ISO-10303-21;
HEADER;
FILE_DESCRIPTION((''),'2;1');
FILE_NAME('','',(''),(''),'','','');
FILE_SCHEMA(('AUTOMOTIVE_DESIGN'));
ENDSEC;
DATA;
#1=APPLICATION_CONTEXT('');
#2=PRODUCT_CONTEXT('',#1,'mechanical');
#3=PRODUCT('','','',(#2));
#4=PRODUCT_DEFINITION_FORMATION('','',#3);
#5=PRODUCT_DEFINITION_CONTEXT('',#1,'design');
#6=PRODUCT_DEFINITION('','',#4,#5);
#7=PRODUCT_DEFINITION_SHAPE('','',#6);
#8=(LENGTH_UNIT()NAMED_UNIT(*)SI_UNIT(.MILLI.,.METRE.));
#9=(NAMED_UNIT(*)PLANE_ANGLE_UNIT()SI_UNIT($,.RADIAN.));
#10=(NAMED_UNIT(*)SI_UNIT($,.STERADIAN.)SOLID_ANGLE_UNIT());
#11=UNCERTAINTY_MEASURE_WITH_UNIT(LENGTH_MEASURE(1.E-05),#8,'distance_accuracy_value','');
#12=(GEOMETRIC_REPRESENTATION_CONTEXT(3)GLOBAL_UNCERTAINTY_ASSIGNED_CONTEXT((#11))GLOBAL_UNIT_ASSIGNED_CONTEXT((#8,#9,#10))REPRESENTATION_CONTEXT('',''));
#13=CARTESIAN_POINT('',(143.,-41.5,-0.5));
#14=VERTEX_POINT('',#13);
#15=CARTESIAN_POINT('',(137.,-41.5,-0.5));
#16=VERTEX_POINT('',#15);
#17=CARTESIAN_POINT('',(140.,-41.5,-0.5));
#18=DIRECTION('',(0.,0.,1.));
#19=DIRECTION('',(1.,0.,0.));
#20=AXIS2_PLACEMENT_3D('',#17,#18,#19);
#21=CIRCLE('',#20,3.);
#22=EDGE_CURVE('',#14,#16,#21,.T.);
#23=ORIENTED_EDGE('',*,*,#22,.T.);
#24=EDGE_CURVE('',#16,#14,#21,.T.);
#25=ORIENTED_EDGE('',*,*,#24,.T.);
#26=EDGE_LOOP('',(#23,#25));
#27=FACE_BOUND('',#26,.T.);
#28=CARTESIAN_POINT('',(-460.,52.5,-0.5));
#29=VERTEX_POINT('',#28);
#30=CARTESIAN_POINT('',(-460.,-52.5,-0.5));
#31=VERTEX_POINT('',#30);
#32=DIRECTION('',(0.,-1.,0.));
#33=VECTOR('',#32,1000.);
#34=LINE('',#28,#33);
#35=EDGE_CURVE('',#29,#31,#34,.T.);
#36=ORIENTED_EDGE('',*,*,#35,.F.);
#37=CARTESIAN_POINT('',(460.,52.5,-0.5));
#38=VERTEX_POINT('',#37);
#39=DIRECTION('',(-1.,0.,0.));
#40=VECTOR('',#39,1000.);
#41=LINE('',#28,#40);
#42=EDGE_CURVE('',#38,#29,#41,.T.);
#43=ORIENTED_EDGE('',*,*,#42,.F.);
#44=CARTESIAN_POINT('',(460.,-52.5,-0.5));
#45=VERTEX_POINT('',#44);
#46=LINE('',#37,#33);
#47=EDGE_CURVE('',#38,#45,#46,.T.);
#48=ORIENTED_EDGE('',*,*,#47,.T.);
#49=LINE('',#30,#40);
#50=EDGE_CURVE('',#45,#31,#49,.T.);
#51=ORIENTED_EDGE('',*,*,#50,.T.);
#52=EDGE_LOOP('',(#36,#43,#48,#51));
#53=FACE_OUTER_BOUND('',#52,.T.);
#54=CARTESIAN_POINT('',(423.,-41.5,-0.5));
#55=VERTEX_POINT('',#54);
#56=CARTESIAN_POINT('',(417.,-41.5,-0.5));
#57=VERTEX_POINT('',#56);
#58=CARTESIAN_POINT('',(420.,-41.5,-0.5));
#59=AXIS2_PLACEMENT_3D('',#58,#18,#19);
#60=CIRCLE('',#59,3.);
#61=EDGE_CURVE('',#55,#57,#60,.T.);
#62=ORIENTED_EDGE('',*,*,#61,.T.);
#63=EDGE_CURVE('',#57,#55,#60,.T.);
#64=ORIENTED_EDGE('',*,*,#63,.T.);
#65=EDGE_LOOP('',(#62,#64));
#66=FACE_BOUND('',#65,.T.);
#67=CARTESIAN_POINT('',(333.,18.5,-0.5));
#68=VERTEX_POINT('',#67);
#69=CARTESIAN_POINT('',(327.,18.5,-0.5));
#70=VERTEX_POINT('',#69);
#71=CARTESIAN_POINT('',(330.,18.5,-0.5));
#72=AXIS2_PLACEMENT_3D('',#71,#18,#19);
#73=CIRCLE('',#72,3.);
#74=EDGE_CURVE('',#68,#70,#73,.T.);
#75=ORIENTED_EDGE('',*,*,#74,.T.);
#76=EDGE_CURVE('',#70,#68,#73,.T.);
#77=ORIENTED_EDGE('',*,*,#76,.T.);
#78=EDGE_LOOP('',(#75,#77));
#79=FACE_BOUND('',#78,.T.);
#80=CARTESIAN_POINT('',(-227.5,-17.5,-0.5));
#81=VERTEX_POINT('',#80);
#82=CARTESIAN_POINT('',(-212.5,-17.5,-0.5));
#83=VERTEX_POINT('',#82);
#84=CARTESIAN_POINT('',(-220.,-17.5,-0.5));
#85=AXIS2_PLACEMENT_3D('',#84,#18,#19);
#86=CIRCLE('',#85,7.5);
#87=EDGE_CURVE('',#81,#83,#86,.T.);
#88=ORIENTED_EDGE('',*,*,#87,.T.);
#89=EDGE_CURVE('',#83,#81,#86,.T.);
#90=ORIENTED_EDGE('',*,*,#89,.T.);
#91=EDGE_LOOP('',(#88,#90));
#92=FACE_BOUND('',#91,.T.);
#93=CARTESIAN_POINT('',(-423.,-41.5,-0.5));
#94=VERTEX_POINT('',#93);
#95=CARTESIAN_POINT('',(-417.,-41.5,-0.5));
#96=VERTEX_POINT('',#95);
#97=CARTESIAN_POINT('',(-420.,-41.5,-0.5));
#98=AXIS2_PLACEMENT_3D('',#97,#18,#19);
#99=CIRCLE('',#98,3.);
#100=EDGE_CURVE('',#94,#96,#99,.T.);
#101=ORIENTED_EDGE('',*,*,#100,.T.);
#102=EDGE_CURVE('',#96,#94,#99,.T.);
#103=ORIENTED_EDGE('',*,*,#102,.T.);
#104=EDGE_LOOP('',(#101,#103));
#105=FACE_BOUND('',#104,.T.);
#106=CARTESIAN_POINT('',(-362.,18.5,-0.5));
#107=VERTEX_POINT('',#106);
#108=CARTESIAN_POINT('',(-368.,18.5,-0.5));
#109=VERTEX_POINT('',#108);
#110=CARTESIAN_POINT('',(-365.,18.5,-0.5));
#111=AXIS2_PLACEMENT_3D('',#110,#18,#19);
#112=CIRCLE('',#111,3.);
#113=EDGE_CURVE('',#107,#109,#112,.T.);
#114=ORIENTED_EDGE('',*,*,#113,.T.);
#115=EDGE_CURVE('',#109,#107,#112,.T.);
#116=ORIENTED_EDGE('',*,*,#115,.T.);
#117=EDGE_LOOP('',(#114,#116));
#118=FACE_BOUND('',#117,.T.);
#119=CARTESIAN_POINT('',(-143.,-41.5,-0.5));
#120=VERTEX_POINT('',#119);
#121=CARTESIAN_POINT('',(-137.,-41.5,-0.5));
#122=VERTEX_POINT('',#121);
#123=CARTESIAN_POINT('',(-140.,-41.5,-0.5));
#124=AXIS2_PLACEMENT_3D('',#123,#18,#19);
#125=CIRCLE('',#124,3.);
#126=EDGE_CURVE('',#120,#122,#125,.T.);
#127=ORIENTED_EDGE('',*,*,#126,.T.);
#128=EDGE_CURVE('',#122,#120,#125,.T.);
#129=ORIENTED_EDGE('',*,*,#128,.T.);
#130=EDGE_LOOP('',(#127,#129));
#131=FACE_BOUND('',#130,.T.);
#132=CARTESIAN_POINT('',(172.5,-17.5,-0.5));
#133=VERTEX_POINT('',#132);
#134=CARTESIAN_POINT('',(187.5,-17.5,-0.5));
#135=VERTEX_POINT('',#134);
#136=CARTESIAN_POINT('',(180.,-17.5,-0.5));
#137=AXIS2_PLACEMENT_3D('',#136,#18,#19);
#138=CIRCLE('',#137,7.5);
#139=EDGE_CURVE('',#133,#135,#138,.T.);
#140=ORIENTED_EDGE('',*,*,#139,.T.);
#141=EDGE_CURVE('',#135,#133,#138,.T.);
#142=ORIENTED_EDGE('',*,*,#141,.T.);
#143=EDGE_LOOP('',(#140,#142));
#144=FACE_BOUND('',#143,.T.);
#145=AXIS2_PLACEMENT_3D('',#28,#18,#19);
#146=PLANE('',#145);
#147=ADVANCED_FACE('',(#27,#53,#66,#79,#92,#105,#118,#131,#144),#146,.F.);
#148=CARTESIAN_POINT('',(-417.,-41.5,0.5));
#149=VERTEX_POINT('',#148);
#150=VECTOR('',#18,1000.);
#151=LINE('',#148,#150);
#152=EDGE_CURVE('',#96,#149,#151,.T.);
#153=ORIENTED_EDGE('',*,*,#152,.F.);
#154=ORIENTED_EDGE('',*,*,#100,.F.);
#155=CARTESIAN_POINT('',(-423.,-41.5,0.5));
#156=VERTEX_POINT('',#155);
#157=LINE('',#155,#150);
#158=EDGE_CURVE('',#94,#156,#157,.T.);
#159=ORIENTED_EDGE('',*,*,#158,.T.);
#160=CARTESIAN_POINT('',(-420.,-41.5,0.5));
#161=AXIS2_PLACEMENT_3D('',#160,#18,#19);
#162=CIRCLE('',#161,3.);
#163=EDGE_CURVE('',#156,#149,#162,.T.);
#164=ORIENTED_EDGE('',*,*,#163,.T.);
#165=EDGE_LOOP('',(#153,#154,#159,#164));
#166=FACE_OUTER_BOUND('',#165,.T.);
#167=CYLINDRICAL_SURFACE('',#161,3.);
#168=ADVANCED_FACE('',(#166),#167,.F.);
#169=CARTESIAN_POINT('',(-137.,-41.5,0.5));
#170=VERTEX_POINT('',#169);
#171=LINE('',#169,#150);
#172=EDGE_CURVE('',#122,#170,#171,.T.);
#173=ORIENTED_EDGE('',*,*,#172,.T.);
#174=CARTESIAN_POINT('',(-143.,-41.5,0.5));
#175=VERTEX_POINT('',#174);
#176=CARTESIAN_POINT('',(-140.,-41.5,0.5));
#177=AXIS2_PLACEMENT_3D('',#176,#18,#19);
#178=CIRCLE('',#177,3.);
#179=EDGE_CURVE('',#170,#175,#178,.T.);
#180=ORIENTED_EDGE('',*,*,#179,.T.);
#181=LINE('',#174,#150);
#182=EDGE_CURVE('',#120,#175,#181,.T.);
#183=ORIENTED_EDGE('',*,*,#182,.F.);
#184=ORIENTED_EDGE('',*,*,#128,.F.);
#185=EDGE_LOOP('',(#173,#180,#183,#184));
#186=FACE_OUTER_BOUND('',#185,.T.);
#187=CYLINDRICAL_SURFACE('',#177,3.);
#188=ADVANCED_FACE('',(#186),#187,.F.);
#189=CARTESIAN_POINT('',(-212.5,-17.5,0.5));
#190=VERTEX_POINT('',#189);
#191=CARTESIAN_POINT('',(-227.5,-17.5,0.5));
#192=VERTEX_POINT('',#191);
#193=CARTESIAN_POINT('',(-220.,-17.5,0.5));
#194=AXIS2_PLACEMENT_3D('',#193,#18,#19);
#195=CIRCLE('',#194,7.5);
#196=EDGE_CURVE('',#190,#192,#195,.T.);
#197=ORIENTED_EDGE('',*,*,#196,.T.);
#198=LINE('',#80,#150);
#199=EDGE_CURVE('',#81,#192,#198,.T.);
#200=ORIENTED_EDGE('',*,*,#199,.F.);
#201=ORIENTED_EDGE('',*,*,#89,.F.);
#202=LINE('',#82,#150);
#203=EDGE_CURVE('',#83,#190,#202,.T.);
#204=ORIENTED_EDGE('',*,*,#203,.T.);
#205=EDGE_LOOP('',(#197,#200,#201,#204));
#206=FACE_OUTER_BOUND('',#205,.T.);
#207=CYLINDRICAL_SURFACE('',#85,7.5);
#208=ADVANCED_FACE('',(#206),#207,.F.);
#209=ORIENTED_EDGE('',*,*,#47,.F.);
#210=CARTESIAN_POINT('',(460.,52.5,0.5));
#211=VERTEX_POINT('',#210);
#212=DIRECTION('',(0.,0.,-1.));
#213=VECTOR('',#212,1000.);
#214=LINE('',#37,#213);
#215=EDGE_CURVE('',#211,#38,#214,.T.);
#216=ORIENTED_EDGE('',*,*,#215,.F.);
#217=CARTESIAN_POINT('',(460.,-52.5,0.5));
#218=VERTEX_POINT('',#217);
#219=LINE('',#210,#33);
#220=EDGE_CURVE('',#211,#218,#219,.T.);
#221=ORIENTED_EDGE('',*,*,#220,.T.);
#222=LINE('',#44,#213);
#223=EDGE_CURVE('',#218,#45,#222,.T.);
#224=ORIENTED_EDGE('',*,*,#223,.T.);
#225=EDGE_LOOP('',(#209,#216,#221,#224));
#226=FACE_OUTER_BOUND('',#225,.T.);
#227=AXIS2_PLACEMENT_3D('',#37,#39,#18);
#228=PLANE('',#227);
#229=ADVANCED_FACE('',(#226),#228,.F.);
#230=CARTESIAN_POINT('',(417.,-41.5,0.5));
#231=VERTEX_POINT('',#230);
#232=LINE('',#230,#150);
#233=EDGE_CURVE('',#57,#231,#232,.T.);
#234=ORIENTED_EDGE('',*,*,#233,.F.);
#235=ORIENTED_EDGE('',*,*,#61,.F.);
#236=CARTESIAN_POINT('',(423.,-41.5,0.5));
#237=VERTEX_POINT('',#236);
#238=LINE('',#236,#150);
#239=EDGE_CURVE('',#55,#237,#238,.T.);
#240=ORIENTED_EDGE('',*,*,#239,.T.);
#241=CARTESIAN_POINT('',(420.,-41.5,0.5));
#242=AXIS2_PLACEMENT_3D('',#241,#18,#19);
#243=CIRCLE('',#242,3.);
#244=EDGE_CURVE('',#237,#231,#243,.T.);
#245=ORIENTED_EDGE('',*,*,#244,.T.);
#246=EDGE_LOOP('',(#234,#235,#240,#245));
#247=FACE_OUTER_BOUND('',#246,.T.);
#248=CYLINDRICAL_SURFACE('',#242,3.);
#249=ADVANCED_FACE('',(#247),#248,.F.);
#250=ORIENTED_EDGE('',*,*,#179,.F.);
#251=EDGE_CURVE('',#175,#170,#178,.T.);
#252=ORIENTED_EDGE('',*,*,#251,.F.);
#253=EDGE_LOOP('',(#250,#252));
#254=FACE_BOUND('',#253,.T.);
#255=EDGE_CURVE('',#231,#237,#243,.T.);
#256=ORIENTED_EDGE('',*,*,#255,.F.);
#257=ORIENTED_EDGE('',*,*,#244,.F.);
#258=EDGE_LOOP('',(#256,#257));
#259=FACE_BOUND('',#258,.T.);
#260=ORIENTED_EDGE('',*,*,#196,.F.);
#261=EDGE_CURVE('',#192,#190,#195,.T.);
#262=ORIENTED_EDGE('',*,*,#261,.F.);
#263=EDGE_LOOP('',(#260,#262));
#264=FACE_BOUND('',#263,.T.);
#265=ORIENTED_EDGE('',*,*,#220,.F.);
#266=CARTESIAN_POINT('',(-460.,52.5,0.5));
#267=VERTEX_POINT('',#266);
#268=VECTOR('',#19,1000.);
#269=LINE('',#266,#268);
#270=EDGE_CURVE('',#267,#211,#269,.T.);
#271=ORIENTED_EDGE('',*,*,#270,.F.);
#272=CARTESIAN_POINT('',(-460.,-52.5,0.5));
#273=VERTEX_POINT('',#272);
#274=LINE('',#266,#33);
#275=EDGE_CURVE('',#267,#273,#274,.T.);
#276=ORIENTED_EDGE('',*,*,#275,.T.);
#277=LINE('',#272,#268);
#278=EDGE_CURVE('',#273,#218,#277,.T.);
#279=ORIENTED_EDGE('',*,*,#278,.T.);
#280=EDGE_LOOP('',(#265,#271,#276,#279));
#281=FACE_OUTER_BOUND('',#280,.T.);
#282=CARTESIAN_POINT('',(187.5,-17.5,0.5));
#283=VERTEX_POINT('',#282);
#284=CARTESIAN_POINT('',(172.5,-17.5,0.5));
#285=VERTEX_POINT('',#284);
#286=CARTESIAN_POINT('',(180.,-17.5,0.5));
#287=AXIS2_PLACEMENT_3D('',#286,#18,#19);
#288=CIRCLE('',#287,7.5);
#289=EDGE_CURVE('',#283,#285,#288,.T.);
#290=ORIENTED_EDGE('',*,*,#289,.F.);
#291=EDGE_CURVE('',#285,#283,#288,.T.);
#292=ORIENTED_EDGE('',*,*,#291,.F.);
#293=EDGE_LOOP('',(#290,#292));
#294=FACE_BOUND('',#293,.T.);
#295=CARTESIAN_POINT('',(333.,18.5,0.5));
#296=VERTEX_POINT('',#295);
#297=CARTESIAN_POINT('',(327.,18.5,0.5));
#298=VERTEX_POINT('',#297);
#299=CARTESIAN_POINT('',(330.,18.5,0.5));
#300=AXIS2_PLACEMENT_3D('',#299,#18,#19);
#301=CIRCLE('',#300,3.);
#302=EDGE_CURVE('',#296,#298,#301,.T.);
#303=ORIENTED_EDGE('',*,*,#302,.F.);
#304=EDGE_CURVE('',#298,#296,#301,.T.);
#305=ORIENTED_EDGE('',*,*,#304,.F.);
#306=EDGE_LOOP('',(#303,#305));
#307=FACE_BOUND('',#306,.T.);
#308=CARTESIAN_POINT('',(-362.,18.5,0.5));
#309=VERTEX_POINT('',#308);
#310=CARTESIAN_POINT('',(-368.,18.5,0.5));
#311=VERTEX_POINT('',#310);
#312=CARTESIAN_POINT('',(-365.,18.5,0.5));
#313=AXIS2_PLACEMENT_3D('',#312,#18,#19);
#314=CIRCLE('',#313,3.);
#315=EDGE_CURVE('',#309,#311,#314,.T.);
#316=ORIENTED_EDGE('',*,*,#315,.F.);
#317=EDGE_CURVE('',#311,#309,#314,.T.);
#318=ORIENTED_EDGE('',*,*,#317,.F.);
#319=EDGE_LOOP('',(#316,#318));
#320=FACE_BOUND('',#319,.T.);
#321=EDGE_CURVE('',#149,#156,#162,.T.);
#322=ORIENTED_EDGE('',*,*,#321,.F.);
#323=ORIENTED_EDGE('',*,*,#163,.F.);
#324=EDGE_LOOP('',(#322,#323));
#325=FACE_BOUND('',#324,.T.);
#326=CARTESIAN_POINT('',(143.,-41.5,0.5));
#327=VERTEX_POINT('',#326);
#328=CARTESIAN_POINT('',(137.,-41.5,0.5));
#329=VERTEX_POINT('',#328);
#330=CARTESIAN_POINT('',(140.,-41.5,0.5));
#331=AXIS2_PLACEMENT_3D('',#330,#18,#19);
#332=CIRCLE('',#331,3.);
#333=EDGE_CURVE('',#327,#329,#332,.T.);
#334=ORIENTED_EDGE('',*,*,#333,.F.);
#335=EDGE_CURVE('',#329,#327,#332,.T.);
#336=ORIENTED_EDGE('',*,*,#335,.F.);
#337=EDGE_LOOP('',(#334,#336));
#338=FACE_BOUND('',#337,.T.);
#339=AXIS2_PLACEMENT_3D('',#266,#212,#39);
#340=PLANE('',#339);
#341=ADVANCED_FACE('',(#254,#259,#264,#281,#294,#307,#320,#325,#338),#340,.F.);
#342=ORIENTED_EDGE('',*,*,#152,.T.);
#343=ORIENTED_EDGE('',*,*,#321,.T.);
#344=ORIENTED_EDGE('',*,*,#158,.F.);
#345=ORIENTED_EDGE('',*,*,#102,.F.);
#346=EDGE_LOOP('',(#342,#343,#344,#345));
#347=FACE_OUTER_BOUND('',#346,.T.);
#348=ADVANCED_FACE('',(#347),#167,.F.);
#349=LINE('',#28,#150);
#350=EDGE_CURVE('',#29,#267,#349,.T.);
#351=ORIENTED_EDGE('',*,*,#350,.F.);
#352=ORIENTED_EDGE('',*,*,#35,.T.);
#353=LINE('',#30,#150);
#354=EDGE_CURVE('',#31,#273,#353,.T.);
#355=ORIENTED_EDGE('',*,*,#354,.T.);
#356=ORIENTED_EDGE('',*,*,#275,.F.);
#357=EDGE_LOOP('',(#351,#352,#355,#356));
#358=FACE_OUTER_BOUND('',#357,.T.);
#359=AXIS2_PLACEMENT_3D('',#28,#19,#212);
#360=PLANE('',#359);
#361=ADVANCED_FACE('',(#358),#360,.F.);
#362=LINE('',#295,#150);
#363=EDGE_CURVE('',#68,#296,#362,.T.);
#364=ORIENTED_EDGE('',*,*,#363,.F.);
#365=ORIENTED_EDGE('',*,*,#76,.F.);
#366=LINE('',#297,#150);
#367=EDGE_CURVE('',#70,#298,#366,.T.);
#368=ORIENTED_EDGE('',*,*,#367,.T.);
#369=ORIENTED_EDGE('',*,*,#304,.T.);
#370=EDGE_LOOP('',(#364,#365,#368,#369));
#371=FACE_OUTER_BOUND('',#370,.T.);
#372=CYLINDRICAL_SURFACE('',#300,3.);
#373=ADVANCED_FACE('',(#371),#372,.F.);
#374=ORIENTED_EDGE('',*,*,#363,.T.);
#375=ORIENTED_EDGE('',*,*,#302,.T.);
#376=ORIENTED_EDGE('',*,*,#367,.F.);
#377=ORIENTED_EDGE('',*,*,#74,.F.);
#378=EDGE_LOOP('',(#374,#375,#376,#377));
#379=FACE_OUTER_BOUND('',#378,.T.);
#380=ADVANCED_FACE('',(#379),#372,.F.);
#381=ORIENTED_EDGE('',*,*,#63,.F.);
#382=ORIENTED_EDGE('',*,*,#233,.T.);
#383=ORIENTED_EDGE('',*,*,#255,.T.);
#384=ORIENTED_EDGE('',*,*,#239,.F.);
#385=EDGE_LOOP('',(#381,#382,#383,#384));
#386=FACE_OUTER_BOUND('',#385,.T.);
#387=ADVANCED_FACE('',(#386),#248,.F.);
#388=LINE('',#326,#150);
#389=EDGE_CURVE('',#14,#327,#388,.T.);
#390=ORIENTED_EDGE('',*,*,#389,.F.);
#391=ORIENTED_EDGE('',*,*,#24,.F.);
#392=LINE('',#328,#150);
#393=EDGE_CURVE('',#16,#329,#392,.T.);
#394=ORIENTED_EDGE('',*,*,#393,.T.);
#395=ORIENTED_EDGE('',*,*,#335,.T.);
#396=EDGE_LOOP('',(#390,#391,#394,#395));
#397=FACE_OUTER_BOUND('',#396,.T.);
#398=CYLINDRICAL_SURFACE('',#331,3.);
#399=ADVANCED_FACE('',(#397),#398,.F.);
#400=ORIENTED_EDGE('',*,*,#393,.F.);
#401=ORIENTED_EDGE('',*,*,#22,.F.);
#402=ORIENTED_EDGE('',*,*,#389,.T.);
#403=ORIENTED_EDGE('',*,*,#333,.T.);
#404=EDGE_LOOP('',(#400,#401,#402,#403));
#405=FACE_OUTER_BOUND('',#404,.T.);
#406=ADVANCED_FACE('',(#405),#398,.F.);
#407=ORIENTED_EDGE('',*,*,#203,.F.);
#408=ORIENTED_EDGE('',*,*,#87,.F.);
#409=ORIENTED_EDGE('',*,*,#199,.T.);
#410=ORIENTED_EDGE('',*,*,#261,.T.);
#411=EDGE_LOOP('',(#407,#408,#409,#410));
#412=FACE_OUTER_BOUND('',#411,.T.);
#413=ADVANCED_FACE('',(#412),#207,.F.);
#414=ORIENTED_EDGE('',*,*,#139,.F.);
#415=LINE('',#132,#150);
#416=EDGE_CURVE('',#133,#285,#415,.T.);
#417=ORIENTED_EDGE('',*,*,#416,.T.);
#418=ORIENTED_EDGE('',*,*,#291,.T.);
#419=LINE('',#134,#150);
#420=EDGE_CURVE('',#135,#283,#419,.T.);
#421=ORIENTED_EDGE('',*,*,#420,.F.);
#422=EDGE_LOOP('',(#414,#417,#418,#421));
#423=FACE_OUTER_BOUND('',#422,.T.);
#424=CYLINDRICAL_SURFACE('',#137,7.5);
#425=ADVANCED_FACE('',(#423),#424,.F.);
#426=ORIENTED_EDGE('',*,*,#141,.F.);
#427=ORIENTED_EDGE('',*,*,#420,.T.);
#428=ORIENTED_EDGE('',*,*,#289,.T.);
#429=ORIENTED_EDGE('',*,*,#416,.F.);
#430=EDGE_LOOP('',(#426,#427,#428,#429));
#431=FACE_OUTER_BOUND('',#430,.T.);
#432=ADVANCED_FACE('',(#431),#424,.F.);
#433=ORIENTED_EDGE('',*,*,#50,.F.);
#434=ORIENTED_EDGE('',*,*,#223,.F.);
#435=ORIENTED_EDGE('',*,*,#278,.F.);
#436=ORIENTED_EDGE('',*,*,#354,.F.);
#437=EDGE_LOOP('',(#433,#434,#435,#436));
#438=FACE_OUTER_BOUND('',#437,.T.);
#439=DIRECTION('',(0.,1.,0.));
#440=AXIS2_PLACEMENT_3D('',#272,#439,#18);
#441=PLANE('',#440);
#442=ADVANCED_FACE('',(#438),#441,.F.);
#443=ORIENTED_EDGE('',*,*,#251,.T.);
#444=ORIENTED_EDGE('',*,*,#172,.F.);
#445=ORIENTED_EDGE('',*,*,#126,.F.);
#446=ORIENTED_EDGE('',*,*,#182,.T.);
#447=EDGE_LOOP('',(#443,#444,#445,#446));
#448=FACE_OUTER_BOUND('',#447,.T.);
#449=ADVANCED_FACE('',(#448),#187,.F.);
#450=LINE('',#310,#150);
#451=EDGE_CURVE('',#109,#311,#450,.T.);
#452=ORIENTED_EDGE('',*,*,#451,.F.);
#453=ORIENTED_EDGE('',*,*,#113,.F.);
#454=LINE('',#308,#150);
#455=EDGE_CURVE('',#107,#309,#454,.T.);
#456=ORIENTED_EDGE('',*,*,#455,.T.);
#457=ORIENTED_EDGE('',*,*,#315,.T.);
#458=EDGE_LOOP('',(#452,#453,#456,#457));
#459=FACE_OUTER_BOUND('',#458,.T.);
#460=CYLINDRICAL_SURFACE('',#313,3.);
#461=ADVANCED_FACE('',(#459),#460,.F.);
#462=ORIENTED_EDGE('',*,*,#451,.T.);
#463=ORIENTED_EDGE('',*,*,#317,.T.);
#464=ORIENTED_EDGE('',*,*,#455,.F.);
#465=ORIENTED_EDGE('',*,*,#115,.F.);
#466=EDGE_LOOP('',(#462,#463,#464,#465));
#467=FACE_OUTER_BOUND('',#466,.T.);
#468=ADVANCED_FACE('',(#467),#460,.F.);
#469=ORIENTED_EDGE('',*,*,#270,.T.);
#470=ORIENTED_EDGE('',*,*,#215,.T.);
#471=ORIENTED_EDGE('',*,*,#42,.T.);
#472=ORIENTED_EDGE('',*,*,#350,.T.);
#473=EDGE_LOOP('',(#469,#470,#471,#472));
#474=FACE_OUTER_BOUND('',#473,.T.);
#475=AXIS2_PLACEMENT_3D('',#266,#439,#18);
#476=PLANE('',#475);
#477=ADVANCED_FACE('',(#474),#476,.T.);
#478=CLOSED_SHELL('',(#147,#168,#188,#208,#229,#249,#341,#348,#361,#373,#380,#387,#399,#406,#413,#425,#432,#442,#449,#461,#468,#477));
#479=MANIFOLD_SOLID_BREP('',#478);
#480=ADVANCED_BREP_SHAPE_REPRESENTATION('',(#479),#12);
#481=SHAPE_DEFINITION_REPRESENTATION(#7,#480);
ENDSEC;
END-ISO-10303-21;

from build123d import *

# Parameters (mm, degrees)
SKETCH1_W                = 920
SKETCH1_H                = 1
EXTRUDE1_DEPTH           = 52.5
SKETCH2_R                = 7.5
CUT_EXTRUDE1_DEPTH       = 463.987310841
M5_CLEARANCE_HOLE1_D     = 6
M5_CLEARANCE_HOLE1_DEPTH = 7
M5_CLEARANCE_HOLE1_TIP   = 1.802581857


with BuildPart() as part:
    # Sketch1 → Extrude1 (new, symmetric)
    with BuildSketch(Plane(origin=(0, 0, 0), x_dir=(1, 0, 0), z_dir=(0, 1, 0))):
        Rectangle(SKETCH1_W, SKETCH1_H)
    extrude(amount=EXTRUDE1_DEPTH, both=True)

    # Sketch2 → Cut-Extrude1 (cut, through all)
    with BuildSketch(Plane.XY.offset(0.5)):
        with Locations((-220, -17.5)):
            Circle(SKETCH2_R)
        with Locations((180, -17.5)):
            Circle(SKETCH2_R)
    extrude(amount=-CUT_EXTRUDE1_DEPTH, mode=Mode.SUBTRACT)

    # M5 Clearance Hole1
    with Locations(Plane.XY.offset(0.5)):
        with Locations((-420, -41.5), (-140, -41.5), (140, -41.5), (-365, 18.5), (330, 18.5), (420, -41.5)):
            Hole(M5_CLEARANCE_HOLE1_D / 2, depth=M5_CLEARANCE_HOLE1_DEPTH)
            with Locations((0, 0, -(M5_CLEARANCE_HOLE1_DEPTH + M5_CLEARANCE_HOLE1_TIP / 2))):  # 118° drill point
                Cone(0, M5_CLEARANCE_HOLE1_D / 2, M5_CLEARANCE_HOLE1_TIP, mode=Mode.SUBTRACT)


solid = part.part
